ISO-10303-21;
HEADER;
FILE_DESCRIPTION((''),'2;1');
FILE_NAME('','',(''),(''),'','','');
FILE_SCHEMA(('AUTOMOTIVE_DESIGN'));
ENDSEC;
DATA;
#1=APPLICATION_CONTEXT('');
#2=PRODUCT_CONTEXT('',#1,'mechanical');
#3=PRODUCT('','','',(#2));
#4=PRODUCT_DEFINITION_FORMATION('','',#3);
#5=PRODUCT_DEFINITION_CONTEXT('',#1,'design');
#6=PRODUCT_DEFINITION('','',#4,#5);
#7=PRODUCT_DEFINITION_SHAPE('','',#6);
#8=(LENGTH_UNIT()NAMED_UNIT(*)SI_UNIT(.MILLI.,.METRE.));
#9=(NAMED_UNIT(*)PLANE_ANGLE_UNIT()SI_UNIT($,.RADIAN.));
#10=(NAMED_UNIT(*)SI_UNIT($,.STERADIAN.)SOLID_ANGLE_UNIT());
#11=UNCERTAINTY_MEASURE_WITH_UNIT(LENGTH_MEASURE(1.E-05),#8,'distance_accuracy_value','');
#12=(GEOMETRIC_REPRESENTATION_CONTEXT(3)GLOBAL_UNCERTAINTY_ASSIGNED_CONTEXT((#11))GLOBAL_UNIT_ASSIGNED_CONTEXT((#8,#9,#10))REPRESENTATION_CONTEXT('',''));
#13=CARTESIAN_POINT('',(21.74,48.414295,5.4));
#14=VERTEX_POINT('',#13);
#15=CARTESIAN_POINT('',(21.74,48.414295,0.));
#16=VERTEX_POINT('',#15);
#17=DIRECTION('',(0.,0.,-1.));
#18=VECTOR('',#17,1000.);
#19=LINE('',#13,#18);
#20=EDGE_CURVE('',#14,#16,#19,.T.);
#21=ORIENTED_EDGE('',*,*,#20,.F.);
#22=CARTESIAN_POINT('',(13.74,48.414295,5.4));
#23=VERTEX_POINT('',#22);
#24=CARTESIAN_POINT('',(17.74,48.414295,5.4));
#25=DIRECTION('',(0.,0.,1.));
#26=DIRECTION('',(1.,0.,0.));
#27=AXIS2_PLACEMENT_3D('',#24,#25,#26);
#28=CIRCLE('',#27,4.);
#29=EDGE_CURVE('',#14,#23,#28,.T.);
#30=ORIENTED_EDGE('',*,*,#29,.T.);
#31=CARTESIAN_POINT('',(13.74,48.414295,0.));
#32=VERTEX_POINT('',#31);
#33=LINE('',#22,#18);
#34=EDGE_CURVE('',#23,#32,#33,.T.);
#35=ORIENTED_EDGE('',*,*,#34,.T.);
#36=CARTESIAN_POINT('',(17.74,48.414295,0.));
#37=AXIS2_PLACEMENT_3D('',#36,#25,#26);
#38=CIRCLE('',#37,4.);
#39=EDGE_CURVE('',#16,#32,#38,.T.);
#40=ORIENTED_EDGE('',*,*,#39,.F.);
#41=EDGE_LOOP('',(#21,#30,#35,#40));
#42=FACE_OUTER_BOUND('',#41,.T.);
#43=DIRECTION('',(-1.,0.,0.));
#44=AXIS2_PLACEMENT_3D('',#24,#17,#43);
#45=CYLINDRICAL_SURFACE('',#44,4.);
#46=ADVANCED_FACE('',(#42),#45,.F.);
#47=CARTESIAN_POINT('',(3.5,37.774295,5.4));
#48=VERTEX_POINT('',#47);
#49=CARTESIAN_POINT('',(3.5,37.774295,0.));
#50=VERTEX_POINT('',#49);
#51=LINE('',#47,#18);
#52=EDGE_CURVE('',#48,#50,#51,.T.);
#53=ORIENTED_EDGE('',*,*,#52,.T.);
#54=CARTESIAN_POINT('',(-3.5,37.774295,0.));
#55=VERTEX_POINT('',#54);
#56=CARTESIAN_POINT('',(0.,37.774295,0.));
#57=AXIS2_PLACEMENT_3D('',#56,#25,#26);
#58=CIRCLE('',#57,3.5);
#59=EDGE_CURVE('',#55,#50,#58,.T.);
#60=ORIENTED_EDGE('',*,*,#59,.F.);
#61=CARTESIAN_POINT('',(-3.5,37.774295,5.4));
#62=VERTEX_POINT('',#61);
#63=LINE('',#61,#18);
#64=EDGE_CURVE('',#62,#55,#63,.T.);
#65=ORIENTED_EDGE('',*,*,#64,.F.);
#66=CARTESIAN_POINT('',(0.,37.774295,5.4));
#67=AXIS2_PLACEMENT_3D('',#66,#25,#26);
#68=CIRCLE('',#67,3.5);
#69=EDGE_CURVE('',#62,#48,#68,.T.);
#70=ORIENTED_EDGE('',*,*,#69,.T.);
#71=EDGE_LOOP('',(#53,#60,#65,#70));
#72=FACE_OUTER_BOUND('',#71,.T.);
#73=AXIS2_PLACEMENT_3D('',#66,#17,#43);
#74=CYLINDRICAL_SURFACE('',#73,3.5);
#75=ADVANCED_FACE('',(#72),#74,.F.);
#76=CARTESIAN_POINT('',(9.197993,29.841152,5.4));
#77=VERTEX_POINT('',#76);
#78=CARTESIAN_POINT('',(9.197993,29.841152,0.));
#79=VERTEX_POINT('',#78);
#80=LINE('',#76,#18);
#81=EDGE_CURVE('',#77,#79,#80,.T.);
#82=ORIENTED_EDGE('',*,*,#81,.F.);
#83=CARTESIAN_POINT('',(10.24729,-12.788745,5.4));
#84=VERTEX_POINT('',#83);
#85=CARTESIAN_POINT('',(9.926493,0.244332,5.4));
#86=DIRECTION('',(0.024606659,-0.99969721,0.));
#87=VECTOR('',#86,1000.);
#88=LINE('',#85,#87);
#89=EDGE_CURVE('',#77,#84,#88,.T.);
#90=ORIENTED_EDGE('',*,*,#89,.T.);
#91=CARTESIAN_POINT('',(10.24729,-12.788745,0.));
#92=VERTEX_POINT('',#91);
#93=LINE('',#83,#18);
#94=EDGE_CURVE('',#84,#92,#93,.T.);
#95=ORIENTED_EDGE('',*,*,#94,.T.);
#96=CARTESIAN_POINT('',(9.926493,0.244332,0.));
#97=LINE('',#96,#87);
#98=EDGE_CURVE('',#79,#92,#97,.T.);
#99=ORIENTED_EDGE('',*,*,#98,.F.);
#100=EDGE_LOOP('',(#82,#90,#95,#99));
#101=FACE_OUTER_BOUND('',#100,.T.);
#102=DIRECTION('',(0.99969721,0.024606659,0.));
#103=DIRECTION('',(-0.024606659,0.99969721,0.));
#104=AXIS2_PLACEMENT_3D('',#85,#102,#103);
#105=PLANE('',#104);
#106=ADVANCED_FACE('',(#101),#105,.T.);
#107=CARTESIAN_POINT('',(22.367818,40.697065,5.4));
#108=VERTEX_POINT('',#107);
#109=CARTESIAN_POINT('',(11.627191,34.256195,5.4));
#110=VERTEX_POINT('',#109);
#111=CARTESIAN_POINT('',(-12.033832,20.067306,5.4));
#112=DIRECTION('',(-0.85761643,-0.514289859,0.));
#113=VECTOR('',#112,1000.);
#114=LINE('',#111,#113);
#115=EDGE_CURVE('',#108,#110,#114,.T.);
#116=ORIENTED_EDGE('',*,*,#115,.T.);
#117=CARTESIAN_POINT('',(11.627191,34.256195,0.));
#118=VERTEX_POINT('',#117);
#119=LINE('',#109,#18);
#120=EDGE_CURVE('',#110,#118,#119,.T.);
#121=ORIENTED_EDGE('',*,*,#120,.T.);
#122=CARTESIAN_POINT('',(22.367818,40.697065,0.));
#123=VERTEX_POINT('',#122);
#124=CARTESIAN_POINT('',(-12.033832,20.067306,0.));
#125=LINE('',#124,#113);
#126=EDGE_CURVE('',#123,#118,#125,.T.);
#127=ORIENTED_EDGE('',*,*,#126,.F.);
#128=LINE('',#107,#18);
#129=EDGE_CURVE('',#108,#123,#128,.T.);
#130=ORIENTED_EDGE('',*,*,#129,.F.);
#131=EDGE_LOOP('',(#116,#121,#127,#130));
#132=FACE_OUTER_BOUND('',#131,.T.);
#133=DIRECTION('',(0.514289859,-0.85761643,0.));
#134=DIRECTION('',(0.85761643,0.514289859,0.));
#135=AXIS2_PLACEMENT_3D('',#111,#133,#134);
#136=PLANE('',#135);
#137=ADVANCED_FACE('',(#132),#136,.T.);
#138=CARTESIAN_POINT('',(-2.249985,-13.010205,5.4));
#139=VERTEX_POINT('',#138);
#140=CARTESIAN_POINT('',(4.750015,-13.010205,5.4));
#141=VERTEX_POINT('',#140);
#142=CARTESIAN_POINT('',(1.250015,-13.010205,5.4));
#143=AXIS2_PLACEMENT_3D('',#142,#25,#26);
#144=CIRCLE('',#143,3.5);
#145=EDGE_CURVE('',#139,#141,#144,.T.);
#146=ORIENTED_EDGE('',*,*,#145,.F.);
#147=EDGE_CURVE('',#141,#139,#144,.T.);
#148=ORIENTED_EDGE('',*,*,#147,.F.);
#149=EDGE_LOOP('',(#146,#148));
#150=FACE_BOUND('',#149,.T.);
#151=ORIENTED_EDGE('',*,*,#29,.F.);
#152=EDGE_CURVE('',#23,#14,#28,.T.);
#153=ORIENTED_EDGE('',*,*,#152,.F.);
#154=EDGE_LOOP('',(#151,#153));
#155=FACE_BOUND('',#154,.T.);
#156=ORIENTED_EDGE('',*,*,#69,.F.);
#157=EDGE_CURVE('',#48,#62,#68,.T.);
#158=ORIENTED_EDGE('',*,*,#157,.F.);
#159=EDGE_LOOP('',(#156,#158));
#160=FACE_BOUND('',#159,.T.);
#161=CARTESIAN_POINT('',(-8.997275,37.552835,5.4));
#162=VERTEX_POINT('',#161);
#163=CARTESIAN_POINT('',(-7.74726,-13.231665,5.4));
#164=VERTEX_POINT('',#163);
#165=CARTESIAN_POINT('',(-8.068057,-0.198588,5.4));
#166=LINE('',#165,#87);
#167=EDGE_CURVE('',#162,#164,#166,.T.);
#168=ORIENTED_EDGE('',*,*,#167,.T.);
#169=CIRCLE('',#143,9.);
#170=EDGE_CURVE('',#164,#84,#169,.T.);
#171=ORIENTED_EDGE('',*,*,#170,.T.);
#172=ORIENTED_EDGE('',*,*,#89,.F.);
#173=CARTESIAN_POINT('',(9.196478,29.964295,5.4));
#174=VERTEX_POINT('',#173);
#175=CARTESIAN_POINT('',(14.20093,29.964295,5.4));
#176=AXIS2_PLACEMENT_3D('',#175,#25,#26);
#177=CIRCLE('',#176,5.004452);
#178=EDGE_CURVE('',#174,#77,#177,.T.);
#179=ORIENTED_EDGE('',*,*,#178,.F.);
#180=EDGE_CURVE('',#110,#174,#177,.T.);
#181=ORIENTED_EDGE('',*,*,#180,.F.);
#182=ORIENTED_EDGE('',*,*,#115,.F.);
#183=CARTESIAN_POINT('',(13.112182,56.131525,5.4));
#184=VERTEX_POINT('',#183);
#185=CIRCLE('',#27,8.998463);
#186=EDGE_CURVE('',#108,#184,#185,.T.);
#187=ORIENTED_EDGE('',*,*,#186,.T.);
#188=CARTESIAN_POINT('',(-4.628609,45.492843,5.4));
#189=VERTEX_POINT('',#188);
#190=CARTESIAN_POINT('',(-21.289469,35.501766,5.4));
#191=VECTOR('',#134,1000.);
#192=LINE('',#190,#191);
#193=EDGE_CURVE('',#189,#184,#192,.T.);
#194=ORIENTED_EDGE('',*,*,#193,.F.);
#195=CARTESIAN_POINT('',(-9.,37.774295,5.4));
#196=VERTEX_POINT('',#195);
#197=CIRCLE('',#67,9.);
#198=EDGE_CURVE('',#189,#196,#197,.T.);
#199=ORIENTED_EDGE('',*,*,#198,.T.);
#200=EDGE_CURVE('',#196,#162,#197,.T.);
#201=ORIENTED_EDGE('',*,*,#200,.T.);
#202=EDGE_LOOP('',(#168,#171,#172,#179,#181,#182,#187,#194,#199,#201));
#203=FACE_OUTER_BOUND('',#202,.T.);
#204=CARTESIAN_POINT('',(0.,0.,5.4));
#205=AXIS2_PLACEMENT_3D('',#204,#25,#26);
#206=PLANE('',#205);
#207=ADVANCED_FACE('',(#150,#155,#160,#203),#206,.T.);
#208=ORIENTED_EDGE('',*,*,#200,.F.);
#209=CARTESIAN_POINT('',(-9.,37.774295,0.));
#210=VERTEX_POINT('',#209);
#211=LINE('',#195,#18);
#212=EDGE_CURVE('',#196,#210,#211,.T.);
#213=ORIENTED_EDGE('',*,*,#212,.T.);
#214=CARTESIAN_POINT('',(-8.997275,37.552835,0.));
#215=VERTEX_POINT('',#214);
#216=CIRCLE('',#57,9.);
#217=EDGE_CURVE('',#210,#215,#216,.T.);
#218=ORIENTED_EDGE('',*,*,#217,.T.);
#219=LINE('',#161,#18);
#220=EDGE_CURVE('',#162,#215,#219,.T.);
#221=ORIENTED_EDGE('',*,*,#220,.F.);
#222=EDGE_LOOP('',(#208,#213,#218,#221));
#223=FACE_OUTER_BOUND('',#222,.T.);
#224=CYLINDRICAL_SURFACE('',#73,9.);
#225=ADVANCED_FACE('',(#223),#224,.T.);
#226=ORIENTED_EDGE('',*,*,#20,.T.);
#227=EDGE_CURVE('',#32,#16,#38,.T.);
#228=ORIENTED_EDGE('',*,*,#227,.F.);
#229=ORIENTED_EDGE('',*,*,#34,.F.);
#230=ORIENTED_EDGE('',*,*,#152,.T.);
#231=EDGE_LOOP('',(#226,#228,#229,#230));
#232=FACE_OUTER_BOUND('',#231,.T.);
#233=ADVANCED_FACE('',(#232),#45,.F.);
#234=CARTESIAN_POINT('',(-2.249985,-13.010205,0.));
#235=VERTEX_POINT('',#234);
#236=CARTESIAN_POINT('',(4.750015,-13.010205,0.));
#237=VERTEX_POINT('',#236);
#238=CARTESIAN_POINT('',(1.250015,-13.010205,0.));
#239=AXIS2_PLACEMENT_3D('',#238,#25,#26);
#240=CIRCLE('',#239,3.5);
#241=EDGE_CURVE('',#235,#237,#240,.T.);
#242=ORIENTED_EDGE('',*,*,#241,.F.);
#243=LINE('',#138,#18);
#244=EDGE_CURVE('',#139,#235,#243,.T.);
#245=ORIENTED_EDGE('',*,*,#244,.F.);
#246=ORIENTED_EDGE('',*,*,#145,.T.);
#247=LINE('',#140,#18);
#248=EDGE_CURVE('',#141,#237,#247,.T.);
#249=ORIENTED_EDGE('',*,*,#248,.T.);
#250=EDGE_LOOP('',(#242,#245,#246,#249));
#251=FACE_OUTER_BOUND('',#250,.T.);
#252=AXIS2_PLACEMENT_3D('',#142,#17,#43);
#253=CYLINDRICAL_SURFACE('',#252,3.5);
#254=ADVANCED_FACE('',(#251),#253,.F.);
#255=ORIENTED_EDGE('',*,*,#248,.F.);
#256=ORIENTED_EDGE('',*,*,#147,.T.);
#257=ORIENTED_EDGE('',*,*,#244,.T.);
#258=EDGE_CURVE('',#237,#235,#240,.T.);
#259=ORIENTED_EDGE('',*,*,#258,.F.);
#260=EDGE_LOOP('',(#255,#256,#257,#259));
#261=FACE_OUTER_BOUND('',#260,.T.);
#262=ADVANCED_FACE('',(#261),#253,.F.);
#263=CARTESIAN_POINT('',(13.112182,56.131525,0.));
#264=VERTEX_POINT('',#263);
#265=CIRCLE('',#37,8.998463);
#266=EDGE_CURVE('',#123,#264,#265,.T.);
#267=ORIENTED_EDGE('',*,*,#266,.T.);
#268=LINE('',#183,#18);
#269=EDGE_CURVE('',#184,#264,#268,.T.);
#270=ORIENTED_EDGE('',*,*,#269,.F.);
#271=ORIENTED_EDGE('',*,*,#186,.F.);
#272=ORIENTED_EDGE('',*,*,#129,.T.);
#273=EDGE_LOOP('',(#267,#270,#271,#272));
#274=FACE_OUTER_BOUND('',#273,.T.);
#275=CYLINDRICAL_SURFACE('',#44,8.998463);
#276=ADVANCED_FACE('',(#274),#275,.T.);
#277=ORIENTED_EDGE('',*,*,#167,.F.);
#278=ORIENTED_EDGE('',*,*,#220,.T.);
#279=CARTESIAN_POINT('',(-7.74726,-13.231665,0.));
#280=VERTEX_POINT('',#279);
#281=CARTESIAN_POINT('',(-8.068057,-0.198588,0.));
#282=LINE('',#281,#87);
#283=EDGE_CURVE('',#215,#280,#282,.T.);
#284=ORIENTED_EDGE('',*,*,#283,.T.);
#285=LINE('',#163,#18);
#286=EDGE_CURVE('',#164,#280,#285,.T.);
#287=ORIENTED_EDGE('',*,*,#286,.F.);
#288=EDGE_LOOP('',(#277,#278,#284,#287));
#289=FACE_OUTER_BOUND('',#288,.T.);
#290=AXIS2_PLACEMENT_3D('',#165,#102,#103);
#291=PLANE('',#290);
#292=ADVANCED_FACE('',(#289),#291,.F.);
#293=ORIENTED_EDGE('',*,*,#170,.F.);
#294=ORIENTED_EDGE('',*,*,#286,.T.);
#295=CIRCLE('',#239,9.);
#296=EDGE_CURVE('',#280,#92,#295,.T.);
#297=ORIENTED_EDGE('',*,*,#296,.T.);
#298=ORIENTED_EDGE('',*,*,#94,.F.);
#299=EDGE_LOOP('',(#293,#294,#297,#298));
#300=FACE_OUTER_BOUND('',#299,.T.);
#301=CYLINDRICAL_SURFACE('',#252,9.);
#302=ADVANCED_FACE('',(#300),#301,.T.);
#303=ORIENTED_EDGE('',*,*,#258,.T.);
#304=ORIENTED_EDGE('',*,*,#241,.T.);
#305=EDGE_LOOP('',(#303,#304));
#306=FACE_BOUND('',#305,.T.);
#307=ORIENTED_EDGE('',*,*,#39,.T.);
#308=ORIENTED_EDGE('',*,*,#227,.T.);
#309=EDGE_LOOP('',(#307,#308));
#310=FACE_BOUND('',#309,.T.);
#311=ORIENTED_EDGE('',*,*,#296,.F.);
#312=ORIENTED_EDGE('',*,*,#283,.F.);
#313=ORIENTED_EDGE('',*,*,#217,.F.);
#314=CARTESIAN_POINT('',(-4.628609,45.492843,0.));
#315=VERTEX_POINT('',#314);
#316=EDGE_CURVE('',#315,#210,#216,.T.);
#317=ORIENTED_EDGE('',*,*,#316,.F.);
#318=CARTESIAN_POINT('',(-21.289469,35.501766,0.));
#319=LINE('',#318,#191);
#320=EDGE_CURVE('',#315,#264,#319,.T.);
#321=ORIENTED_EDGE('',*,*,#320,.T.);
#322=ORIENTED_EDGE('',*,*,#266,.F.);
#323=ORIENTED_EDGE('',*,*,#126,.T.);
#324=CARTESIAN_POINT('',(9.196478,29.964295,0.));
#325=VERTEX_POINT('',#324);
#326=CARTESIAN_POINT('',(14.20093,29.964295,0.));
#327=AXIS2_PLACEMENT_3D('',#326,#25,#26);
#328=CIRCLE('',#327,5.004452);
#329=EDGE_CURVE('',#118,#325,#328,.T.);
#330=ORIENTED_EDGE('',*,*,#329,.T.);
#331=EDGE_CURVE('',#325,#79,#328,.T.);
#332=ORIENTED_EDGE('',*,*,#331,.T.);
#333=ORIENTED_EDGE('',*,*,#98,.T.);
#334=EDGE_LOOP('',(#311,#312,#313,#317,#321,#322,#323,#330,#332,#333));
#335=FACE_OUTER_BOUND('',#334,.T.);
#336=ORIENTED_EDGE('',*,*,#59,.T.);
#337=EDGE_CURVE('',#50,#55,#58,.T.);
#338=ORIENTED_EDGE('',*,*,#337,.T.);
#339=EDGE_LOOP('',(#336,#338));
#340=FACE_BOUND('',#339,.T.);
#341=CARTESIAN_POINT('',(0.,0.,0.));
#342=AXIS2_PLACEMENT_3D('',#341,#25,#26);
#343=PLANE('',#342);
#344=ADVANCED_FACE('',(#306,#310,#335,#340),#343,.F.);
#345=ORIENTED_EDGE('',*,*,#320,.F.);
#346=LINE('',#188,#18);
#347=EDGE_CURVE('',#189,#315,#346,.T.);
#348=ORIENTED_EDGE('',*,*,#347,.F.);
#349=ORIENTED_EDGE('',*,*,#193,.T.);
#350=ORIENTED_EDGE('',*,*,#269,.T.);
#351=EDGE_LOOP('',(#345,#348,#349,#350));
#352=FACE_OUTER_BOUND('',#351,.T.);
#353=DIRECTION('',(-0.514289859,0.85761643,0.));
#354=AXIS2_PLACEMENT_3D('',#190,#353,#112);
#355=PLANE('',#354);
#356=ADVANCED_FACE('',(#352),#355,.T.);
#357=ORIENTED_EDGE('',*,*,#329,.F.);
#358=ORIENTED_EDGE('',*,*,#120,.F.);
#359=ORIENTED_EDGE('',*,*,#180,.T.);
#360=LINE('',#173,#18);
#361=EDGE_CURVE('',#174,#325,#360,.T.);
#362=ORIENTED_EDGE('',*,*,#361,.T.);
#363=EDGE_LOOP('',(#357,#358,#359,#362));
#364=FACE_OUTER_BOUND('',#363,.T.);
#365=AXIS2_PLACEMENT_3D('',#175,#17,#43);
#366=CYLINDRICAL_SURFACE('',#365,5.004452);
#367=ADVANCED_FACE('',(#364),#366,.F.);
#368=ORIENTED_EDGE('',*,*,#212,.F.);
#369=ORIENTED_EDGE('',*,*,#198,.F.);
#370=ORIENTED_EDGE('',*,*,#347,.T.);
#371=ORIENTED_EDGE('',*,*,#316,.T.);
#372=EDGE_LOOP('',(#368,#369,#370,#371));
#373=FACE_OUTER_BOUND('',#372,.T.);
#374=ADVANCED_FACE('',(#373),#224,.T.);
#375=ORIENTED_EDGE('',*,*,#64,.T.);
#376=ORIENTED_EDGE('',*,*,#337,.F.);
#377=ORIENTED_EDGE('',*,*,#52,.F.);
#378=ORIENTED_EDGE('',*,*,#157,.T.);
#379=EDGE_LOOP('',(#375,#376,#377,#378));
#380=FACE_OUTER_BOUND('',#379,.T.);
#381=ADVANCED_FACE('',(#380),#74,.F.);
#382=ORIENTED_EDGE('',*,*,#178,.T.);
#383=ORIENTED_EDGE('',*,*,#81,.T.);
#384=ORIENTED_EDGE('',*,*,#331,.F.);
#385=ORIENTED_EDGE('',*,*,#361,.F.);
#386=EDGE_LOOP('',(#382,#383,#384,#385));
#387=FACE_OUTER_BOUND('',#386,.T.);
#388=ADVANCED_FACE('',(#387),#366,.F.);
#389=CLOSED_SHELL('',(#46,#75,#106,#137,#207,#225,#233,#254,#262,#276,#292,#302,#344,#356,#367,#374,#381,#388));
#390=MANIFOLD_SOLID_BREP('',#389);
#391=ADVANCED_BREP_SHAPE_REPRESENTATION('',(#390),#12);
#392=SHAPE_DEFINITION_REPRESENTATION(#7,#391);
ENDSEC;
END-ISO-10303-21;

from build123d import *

# Parameters (mm, degrees)
SKETCH1_R           = 3.5
SKETCH1_R_2         = 4
BOSS_EXTRUDE1_DEPTH = 5.4


with BuildPart() as part:
    # Sketch1 → Boss-Extrude1 (new body)
    with BuildSketch(Plane.XY):
        with BuildLine():
            Line((-8.997274893, 37.552834761), (-7.747259547, -13.231665239))
            ThreePointArc((-7.747259547, -13.231665239), (1.471475273, -22.007480205), (10.247290239, -12.788745384))
            Line((10.247290239, -12.788745384), (9.197993195, 29.841151848))
            ThreePointArc((9.197993195, 29.841151848), (9.816337009, 32.376738458), (11.627190957, 34.256194898))
            Line((11.627190957, 34.256194898), (22.36781842, 40.697064727))
            ThreePointArc((22.36781842, 40.697064727), (25.457229961, 53.042113109), (13.11218158, 56.13152465))
            Line((13.11218158, 56.13152465), (-4.628608734, 45.492842556))
            ThreePointArc((-4.628608734, 45.492842556), (-7.885246166, 42.11283049), (-8.997274893, 37.552834761))
        make_face()
        with Locations(Location((0, 37.774294688, 0), (0, 0, 180))):
            Circle(SKETCH1_R, mode=Mode.SUBTRACT)
        with Locations(Location((1.250015346, -13.010205312, 0), (0, 0, 180))):
            Circle(SKETCH1_R, mode=Mode.SUBTRACT)
        with Locations(Location((17.74, 48.414294688, 0), (0, 0, 180))):
            Circle(SKETCH1_R_2, mode=Mode.SUBTRACT)
    extrude(amount=BOSS_EXTRUDE1_DEPTH)


solid = part.part
